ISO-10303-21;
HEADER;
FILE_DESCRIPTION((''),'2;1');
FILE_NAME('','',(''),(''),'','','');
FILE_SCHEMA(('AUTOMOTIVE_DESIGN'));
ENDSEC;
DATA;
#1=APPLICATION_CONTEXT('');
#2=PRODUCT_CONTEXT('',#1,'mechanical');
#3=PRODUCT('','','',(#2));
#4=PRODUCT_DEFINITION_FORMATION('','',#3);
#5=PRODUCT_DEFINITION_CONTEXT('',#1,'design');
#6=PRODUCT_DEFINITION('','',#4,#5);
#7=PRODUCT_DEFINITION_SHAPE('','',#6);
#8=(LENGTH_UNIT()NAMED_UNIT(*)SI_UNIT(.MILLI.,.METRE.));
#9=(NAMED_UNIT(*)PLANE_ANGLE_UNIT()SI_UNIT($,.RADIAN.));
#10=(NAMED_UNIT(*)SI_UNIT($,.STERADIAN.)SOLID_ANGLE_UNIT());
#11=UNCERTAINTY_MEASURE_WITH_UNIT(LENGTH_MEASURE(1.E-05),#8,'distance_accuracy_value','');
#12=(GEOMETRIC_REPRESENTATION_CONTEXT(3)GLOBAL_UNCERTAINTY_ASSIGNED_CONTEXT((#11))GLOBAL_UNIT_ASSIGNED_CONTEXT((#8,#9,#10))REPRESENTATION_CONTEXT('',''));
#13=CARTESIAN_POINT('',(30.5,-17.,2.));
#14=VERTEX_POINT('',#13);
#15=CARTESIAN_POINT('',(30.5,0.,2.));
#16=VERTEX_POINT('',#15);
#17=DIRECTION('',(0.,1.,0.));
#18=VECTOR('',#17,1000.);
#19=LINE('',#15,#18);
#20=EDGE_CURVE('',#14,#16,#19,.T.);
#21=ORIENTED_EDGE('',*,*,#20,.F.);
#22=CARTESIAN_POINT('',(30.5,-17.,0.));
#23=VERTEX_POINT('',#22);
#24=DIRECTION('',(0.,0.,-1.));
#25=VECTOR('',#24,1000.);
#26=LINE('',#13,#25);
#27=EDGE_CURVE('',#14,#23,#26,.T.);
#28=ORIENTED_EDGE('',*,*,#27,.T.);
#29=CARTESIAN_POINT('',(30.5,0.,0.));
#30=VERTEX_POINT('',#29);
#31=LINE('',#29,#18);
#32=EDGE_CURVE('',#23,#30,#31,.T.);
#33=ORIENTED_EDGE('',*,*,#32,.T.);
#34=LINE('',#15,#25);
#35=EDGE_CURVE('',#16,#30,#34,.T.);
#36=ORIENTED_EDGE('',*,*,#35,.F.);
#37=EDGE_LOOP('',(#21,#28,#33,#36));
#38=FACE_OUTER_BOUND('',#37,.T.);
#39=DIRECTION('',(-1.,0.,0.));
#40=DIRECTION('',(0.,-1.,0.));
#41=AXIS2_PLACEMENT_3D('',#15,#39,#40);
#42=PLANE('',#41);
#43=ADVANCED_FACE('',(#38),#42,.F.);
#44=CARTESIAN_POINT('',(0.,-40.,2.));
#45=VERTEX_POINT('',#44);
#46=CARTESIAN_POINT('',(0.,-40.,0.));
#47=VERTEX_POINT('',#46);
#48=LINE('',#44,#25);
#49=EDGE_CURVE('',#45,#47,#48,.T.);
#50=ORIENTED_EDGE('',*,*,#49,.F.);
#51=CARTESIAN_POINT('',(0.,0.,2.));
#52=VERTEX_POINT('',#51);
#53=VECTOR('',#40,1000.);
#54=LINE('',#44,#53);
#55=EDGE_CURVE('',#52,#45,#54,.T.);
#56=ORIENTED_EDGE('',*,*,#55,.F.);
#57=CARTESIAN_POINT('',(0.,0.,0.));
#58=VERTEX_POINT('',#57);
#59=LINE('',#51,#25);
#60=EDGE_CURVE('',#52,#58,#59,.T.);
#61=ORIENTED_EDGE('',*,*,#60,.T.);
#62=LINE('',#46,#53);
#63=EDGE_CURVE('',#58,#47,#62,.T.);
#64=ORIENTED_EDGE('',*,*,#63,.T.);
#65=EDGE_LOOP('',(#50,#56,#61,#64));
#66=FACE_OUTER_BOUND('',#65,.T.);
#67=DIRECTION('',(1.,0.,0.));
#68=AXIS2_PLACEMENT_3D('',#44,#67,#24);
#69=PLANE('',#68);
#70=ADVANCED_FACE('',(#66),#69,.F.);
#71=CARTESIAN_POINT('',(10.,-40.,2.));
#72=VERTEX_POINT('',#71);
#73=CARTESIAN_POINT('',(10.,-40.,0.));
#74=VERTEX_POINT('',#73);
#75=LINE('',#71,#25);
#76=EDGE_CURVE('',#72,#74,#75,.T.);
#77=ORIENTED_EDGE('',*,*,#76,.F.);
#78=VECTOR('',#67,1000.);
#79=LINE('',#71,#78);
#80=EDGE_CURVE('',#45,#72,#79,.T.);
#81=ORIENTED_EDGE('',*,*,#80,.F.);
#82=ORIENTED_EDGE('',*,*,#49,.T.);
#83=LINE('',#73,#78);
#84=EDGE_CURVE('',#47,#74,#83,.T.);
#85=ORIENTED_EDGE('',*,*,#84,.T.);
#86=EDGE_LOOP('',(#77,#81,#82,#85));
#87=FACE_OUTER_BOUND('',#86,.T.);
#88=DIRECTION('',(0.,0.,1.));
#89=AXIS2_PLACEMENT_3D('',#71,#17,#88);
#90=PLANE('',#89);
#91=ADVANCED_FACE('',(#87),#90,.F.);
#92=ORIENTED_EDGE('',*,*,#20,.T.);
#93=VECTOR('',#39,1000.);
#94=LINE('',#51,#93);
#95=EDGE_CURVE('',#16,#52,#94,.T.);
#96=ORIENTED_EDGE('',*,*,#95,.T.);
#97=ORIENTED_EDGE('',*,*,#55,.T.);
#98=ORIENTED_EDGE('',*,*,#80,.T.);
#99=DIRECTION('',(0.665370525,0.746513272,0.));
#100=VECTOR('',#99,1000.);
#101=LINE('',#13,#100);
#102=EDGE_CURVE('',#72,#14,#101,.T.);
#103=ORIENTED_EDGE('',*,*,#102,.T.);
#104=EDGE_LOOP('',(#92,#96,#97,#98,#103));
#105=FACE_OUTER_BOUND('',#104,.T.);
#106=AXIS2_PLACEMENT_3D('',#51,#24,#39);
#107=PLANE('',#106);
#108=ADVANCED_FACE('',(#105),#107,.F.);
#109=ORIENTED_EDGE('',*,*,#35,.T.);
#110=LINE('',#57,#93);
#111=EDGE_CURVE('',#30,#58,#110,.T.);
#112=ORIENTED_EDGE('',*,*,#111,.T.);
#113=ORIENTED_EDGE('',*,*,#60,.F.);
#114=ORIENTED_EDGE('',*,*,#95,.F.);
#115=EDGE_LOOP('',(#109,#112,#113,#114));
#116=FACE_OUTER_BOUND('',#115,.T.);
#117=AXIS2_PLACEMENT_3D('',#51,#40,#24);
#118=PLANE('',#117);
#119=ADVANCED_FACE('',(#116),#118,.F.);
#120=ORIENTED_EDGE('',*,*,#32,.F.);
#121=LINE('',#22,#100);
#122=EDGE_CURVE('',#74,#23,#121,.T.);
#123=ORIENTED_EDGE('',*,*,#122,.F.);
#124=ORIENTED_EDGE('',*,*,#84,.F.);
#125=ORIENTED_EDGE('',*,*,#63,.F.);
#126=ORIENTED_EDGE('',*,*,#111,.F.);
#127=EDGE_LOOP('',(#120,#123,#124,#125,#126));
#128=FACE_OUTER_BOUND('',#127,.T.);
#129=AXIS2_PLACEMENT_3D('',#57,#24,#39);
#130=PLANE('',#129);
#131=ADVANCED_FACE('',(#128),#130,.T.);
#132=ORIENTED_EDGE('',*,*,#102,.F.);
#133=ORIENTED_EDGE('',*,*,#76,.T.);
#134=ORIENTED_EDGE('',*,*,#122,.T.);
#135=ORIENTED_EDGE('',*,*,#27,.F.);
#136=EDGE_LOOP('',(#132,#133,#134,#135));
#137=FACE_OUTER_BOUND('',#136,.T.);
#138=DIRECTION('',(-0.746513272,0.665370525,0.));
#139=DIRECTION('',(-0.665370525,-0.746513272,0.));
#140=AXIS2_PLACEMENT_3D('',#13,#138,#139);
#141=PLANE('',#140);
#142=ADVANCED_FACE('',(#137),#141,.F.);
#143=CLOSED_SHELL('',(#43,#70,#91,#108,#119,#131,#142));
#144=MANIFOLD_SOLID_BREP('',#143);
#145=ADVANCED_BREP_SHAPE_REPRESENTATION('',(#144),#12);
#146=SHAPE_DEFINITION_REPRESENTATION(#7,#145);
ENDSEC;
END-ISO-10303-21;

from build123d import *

# Parameters (mm, degrees)
EXTRUDE_1_DEPTH = 2


with BuildPart() as part:
    # 草图1 → 凸台-拉伸1 (new body)
    with BuildSketch(Plane.XY):
        Polygon((0, 0), (30.5, 0), (30.5, -17), (10, -40), (0, -40), align=None)
    extrude(amount=EXTRUDE_1_DEPTH)


solid = part.part
